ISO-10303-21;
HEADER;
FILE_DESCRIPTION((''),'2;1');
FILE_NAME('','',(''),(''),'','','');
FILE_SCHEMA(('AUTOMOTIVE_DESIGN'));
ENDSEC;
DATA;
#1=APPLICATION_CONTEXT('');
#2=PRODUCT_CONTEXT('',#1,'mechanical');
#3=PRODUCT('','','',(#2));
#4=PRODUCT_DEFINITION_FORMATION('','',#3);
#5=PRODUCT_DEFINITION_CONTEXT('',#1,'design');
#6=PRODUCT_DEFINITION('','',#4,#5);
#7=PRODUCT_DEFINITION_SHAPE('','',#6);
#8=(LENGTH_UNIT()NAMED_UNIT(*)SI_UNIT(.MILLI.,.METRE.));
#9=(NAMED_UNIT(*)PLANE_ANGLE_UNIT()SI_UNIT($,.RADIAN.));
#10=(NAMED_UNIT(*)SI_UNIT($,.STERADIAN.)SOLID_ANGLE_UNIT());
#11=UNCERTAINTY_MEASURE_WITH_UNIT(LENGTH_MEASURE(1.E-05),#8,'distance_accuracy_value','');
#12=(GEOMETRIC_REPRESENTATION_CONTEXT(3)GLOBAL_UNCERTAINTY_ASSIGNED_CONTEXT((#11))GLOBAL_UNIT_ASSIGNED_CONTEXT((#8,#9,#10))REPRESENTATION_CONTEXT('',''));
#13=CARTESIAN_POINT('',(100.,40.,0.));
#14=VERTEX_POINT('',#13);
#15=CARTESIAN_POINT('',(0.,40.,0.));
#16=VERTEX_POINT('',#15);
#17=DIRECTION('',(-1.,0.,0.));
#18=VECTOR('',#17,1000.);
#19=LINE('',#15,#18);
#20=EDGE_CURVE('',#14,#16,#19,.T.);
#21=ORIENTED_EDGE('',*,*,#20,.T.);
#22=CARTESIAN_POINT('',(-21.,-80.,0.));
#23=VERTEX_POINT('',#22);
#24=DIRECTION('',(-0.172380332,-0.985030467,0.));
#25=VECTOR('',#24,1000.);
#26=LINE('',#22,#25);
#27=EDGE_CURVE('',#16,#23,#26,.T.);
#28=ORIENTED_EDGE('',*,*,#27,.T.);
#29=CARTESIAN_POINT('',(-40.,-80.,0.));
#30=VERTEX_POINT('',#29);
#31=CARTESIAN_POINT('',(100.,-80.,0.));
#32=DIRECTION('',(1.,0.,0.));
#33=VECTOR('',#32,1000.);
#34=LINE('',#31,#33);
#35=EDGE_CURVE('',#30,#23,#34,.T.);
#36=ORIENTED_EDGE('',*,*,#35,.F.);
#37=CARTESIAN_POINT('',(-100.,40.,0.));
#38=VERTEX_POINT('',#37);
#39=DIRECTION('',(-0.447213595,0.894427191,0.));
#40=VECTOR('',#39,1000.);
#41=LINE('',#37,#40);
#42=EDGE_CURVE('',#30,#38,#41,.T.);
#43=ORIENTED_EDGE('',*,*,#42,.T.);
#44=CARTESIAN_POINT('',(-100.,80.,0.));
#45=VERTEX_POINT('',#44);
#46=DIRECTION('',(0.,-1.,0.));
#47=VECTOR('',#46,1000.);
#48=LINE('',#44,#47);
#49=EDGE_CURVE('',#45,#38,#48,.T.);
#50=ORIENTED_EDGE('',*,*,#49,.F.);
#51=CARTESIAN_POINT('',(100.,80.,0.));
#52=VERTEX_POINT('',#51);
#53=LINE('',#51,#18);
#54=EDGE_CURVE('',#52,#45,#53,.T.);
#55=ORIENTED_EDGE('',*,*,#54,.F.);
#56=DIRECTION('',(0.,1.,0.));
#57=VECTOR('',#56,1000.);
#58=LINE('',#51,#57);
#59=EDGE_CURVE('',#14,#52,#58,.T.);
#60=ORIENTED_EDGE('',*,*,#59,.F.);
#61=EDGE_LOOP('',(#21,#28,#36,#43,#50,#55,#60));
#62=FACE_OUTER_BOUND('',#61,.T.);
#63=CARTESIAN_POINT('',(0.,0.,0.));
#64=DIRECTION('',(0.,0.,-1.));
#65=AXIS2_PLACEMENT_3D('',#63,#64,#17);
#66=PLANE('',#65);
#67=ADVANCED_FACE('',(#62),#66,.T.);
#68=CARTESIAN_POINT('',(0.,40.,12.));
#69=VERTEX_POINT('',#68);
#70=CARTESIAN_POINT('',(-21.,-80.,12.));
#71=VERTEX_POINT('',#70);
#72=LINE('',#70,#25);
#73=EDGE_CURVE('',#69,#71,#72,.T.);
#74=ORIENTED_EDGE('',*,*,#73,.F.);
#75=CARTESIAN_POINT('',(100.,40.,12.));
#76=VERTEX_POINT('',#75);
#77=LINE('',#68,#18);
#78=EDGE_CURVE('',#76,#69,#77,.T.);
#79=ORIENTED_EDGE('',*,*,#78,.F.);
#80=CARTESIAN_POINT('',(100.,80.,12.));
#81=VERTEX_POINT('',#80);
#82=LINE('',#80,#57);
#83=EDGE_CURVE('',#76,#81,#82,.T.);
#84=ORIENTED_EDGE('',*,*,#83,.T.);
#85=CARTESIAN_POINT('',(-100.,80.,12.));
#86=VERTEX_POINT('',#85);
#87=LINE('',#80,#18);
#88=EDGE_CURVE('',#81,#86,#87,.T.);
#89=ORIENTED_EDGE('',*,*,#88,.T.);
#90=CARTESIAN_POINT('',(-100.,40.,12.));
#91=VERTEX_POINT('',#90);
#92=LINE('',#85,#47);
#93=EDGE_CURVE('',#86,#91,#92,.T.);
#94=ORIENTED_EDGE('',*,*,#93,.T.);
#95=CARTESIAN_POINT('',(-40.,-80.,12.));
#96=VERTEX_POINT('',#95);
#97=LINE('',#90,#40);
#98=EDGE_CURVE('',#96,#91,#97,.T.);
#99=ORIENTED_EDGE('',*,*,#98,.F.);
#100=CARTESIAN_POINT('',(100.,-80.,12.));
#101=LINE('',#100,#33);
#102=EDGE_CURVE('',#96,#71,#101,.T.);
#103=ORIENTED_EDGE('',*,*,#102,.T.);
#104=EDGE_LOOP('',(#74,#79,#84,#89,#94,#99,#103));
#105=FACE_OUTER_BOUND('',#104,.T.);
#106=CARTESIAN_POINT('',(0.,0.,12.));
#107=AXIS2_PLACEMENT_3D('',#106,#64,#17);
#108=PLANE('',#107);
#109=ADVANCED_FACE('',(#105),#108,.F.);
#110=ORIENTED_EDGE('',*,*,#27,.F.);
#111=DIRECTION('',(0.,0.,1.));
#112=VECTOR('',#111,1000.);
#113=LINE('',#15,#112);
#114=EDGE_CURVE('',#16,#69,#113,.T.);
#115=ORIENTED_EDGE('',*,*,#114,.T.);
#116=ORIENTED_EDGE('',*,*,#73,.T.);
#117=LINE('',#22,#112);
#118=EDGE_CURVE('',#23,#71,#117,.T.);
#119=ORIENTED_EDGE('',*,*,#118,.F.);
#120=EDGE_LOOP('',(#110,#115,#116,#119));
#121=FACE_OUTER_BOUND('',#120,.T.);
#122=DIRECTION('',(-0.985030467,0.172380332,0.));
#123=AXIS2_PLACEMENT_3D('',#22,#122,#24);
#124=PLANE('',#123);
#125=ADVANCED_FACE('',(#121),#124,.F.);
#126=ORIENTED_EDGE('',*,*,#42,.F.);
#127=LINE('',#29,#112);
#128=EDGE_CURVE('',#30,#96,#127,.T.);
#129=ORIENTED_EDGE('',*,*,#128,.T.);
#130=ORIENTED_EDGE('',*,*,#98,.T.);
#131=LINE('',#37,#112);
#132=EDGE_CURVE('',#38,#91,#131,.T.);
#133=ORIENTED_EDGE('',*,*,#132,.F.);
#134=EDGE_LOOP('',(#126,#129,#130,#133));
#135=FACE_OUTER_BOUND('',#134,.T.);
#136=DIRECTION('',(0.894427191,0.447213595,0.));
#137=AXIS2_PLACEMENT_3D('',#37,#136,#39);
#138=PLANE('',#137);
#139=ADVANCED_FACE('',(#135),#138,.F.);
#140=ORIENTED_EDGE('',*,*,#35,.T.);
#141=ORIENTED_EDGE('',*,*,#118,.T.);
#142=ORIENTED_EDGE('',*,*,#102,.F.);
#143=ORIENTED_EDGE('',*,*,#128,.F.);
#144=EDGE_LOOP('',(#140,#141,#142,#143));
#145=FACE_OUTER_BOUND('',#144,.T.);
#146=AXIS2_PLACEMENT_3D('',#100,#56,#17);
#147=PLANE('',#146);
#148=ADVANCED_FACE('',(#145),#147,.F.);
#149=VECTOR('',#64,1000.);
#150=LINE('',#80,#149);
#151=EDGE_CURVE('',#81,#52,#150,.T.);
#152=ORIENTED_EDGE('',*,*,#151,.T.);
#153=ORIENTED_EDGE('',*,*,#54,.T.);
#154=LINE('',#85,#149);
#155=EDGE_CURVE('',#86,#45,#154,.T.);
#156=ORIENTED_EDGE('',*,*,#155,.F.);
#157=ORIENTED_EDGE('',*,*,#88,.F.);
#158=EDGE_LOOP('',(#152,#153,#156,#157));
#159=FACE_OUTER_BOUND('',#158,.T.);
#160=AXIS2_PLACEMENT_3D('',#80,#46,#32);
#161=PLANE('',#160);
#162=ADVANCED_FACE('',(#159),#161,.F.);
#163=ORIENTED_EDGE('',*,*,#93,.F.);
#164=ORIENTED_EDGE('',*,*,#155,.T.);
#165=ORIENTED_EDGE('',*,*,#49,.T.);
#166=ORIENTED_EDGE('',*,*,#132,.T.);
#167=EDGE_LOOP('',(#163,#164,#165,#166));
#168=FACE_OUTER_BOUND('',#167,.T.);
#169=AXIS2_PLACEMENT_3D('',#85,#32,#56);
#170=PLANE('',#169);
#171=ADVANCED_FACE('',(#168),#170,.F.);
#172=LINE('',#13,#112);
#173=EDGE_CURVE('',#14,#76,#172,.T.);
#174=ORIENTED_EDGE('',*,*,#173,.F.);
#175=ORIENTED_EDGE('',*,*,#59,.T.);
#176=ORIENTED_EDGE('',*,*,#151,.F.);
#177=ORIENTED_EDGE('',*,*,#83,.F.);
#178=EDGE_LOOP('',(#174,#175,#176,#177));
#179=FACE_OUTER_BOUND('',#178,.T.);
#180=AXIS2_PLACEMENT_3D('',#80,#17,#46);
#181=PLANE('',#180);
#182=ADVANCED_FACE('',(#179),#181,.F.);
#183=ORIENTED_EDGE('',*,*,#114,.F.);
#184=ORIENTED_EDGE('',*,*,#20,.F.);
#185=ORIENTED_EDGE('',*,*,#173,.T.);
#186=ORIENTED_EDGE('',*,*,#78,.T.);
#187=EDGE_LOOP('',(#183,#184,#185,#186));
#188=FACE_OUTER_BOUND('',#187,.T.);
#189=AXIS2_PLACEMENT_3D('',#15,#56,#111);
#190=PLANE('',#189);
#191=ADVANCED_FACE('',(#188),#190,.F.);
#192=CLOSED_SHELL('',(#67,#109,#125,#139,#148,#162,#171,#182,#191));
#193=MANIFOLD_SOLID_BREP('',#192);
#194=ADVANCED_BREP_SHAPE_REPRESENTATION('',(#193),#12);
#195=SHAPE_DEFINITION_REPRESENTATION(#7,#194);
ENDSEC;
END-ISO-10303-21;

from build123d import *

# Parameters (mm, degrees)
SKETCH_1_W          = 200
SKETCH_1_H          = 160
EXTRUDE_1_DEPTH     = 12
CUT_EXTRUDE_1_DEPTH = 12


with BuildPart() as part:
    # 草图1 → 凸台-拉伸1 (new body)
    with BuildSketch(Plane.XY):
        Rectangle(SKETCH_1_W, SKETCH_1_H)
    extrude(amount=EXTRUDE_1_DEPTH)

    # 草图2 → 切除-拉伸1 (cut)
    with BuildSketch(Plane.XY.offset(12)):
        Polygon((-100, 40), (-40, -80), (-100, -80), align=None)
        Polygon((-21, -80), (0, 40), (100, 40), (100, -80), align=None)
    extrude(amount=-CUT_EXTRUDE_1_DEPTH, mode=Mode.SUBTRACT)


solid = part.part
